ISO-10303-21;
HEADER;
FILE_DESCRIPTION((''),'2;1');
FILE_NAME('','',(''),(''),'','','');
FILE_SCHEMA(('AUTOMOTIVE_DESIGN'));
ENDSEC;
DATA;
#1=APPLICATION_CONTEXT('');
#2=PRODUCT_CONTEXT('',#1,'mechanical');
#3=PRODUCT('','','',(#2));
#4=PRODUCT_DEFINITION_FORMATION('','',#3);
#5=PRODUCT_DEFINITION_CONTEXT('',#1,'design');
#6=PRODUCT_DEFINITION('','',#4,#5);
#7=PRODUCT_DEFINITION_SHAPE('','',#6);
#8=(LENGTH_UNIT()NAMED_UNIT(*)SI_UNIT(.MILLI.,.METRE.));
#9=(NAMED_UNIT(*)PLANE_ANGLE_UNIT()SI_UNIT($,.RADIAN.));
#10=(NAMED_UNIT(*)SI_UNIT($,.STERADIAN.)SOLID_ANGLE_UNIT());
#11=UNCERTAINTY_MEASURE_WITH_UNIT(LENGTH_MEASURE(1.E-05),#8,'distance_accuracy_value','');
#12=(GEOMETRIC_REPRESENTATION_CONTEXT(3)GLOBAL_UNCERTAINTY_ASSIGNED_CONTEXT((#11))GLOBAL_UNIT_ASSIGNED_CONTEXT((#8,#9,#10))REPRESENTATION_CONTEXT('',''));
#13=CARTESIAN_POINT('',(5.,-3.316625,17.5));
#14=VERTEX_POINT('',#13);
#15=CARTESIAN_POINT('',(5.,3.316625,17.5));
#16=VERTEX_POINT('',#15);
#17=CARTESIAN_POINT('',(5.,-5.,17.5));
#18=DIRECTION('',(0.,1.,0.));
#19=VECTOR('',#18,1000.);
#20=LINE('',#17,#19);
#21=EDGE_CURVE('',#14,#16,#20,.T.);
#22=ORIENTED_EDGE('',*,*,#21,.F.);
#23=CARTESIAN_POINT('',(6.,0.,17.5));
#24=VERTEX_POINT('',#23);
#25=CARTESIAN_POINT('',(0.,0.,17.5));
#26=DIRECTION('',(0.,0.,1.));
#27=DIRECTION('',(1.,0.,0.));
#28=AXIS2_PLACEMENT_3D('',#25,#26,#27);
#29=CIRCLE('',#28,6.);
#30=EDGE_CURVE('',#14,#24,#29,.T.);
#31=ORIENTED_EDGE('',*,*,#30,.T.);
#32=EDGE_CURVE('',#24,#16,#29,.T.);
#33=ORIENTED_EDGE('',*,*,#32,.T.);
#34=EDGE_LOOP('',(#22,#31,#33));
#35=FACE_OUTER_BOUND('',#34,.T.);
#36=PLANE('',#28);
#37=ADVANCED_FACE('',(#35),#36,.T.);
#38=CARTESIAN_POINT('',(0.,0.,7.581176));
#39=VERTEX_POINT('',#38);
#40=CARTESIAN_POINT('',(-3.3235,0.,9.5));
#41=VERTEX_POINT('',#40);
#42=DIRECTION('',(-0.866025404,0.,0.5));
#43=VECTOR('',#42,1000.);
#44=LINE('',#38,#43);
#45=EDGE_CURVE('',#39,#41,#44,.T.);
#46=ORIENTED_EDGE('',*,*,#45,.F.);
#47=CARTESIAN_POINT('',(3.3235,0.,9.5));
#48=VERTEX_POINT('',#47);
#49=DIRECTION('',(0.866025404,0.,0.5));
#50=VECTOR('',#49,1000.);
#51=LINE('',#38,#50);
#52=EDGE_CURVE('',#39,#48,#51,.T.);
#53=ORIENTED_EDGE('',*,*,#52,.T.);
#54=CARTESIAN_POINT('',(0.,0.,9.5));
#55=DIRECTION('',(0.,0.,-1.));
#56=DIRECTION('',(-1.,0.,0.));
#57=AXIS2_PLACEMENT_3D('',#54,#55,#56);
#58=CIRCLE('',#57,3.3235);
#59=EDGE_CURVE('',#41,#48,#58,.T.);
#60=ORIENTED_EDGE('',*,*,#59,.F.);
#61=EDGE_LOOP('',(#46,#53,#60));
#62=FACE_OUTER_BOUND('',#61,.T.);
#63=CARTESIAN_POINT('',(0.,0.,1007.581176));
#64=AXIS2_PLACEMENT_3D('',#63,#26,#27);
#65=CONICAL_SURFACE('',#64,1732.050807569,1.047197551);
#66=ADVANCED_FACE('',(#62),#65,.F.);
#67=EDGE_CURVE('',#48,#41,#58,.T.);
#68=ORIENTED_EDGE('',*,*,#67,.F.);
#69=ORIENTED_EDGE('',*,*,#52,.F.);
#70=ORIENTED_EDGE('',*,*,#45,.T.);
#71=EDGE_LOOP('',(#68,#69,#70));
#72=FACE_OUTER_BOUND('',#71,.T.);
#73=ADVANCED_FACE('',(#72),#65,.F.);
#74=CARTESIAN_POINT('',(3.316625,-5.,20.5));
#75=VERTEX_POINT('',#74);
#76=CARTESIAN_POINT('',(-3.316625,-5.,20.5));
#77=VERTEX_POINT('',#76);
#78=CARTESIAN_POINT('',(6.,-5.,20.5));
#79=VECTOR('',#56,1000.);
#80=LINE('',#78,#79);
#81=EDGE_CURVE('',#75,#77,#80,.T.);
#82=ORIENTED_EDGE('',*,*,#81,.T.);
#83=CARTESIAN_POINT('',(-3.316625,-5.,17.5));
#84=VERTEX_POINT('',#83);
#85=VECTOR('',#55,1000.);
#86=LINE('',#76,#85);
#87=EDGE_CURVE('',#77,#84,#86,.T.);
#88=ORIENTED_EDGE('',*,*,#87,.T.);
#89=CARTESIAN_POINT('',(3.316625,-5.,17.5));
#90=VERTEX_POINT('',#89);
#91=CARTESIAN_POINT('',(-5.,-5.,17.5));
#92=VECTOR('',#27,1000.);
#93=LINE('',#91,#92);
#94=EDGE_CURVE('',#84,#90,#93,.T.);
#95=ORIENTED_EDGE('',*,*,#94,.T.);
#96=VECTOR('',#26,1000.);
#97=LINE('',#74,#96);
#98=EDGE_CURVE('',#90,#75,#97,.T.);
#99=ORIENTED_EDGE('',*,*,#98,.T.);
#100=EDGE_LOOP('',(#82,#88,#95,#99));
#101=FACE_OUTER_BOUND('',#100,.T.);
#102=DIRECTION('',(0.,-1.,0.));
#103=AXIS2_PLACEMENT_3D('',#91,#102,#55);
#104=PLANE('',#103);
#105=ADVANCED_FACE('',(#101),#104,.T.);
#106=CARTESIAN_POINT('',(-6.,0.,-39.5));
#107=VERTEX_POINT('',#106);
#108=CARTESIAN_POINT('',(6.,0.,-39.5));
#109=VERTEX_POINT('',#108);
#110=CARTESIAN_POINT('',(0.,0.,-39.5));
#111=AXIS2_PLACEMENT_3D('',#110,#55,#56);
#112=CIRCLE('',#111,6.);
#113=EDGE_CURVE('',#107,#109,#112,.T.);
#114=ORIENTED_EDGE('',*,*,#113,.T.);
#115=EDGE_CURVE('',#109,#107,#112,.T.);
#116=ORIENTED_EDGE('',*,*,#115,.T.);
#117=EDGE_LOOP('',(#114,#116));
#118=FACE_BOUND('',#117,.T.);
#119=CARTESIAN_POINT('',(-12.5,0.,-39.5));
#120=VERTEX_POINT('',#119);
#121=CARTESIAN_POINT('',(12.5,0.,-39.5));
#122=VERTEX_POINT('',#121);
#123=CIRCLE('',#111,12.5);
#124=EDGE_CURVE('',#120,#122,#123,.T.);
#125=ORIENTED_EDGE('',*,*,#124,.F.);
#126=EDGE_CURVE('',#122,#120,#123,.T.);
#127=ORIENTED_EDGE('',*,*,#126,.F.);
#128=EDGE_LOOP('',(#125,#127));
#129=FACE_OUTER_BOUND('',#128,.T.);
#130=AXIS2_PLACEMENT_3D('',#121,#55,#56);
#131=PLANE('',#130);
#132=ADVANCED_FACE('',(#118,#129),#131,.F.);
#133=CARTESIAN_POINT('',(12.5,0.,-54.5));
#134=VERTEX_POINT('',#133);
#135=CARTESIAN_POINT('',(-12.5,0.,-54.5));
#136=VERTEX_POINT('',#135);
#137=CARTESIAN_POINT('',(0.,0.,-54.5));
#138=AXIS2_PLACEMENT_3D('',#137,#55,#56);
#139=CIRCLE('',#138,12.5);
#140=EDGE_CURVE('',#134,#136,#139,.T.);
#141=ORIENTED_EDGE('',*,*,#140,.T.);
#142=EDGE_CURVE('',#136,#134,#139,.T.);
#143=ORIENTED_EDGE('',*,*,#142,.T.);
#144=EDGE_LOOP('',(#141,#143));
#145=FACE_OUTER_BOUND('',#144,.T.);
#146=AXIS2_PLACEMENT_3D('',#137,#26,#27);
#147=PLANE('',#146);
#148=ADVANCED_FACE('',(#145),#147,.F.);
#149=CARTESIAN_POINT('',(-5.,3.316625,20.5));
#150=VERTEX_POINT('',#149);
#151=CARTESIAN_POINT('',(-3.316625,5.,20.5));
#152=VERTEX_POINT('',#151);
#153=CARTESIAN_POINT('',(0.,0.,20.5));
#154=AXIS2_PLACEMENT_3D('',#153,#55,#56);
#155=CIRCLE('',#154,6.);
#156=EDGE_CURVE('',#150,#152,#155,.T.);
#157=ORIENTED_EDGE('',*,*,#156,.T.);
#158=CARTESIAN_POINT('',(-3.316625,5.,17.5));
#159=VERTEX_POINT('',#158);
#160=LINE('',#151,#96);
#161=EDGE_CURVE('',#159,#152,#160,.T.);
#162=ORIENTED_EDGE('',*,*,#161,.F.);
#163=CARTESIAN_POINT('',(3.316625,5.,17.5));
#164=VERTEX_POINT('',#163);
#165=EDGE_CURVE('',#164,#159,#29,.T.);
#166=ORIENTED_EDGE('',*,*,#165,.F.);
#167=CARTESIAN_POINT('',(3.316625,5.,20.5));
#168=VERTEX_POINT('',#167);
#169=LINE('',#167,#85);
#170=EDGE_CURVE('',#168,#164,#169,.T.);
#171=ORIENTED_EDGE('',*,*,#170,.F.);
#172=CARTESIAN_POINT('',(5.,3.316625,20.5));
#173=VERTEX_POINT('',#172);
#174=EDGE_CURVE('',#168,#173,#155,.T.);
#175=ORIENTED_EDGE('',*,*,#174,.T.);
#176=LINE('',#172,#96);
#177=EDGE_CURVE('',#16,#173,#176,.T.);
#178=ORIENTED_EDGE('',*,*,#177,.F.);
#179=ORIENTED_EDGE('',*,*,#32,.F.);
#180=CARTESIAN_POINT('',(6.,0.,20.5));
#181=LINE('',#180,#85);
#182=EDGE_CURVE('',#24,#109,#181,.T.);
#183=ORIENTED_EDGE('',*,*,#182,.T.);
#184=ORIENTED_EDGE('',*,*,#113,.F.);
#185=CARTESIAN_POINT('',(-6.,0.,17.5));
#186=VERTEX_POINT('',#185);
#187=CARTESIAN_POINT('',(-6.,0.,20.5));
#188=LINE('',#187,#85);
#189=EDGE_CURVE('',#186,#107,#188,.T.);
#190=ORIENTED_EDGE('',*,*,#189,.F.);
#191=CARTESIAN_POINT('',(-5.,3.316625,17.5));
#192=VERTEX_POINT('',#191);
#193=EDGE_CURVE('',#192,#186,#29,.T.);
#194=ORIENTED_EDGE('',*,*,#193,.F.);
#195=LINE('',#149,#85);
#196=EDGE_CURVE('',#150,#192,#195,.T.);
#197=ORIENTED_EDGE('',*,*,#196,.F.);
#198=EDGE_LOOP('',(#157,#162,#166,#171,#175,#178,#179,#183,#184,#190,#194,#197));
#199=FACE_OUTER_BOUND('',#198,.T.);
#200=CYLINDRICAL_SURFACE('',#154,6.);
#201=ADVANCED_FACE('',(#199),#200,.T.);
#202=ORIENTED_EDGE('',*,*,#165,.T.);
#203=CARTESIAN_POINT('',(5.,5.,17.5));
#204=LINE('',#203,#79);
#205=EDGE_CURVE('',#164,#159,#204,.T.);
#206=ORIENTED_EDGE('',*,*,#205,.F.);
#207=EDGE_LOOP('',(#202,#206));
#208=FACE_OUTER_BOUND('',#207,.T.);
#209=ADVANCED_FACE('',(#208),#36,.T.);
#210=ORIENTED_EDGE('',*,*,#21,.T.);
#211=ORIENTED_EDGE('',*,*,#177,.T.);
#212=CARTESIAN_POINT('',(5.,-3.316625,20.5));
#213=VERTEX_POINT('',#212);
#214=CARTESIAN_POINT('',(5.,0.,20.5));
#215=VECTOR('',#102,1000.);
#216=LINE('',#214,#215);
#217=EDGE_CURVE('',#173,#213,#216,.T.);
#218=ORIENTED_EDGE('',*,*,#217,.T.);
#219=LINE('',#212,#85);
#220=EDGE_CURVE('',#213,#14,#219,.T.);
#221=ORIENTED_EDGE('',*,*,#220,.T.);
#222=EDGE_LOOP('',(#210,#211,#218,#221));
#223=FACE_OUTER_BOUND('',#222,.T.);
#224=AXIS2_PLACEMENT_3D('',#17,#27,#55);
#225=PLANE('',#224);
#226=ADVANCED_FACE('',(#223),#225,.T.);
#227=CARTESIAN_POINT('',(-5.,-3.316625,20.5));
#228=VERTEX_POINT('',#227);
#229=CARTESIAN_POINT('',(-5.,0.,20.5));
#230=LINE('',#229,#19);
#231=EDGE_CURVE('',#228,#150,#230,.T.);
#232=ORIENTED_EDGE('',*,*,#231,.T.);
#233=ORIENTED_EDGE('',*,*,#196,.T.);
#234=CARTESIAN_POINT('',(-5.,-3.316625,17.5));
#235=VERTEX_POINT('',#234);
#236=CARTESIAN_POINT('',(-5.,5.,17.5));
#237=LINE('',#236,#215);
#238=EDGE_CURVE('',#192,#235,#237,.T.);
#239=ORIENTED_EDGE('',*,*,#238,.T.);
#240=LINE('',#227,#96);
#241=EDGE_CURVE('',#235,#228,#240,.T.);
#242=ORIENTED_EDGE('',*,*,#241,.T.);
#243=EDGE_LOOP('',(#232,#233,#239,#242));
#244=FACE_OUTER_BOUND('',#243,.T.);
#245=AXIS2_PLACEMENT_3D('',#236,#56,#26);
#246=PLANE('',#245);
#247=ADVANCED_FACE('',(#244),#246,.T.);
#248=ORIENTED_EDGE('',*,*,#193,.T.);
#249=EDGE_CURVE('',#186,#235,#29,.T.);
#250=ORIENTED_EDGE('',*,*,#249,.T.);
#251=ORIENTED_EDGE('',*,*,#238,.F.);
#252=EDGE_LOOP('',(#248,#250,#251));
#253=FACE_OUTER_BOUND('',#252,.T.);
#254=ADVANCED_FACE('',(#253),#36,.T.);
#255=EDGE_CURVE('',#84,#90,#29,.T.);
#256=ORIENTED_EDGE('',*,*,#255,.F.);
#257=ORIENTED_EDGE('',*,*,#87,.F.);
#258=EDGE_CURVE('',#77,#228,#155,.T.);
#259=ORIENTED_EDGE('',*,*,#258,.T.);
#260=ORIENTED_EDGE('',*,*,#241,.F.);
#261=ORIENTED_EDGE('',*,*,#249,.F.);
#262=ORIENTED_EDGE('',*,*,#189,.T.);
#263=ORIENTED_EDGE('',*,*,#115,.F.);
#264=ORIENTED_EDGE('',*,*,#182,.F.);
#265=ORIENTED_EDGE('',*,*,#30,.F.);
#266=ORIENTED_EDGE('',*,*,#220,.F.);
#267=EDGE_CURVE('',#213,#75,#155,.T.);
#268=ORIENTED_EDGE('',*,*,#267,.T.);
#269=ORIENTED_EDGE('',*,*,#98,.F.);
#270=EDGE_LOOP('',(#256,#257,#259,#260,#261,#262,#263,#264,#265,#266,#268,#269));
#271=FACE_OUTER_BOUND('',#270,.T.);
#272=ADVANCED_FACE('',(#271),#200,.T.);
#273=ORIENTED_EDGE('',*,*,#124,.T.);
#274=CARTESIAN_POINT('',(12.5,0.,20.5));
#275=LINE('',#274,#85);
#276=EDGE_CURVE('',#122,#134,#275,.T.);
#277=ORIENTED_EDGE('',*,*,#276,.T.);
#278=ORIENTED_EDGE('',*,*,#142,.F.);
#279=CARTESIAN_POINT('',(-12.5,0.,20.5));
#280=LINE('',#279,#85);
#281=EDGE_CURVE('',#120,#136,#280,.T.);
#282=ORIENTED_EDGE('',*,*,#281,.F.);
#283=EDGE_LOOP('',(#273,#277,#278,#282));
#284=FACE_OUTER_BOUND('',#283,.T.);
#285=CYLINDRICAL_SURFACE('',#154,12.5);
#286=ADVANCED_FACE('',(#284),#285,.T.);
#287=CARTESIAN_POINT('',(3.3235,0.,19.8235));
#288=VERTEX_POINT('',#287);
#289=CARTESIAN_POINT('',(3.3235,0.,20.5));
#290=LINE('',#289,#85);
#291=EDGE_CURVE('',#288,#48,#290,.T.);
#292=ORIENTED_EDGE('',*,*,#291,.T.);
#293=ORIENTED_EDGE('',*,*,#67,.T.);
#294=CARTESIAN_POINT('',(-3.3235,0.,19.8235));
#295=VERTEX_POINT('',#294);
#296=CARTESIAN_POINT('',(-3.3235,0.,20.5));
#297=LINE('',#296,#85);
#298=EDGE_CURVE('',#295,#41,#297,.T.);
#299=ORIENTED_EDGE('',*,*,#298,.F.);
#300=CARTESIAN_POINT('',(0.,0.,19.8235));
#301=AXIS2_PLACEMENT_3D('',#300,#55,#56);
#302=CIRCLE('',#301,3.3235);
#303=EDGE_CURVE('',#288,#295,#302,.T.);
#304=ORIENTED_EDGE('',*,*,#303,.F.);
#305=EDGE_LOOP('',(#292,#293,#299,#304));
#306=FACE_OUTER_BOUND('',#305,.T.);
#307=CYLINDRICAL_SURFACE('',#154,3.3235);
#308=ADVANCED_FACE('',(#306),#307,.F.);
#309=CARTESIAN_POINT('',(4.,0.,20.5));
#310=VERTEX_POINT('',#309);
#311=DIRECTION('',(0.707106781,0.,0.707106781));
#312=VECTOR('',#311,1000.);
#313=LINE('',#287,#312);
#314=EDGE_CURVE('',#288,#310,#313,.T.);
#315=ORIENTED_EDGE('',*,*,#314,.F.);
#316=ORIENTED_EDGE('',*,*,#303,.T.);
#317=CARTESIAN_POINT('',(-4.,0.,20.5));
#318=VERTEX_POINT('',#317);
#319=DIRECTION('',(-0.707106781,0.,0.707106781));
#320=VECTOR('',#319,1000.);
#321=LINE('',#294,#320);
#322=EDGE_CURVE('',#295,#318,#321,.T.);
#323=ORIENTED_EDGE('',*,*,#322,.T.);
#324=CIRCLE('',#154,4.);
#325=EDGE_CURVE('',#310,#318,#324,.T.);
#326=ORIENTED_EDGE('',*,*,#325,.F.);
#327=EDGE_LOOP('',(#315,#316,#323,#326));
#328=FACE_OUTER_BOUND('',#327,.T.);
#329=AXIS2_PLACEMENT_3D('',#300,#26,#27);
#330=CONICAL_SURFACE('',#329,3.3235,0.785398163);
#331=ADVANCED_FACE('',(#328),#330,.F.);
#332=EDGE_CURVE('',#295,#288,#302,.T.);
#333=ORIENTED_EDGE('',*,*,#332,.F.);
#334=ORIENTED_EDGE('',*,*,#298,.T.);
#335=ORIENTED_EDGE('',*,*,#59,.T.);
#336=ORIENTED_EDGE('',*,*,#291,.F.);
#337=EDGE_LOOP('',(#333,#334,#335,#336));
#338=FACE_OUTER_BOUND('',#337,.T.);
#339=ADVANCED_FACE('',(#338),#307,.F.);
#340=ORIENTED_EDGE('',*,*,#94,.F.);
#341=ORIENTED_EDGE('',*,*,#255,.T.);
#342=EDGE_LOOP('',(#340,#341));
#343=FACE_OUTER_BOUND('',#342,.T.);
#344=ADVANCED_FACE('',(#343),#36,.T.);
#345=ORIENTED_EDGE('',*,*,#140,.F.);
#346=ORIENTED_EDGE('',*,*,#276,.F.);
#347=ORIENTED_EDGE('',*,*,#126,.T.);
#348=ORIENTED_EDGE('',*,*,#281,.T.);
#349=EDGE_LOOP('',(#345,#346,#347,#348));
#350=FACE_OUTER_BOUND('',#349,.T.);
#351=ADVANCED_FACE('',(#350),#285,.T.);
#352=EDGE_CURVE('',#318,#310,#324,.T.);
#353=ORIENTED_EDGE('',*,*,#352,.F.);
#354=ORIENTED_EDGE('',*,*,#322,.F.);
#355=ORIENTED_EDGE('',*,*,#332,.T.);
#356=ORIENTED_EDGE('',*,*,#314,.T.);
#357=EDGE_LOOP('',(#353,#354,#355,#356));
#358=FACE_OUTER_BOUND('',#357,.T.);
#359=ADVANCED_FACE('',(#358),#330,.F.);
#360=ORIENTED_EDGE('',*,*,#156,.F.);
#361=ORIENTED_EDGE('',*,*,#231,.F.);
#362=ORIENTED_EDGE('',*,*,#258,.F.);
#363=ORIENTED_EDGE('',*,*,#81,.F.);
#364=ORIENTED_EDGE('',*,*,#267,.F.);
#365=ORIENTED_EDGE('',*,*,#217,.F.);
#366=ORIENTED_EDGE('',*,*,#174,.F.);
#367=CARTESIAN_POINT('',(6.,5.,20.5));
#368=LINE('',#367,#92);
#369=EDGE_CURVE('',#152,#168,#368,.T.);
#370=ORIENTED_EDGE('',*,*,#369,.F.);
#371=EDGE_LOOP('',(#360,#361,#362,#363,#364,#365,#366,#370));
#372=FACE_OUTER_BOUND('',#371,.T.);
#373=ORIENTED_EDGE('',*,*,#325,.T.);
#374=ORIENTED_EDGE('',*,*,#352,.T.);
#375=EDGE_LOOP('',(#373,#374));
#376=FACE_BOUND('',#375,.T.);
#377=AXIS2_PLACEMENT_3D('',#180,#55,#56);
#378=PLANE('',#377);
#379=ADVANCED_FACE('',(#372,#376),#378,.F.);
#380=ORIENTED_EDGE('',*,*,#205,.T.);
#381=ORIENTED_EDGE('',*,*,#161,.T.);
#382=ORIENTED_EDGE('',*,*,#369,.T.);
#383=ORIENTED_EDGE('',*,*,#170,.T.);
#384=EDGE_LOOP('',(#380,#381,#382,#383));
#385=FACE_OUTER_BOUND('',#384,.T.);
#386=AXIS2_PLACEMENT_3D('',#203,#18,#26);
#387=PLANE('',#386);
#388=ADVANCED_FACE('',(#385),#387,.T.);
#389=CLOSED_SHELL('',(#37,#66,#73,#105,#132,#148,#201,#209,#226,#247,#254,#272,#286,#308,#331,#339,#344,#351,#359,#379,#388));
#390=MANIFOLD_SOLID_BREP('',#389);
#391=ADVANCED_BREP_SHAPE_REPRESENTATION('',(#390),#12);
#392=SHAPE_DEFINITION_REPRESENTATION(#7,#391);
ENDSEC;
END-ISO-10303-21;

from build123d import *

# Parameters (mm, degrees)
SKETCH_2_R          = 10
SKETCH_2_W          = 10
SKETCH_2_H          = 10
CUT_EXTRUDE_1_DEPTH = 3


with BuildPart() as part:
    # 草图1 → 旋转1 (revolve)
    with BuildSketch(Plane(origin=(0, 0, 0), x_dir=(1, 0, 0), z_dir=(0, 1, 0)), mode=Mode.PRIVATE) as revolve_1_sk:
        Polygon((0, 54.5), (12.5, 54.5), (12.5, 39.5), (6, 39.5), (6, -20.5), (4, -20.5), (3.3235, -19.8235), (3.3235, -9.5), (0, -7.58117638), align=None)
    revolve(revolve_1_sk.sketch.rotate(Axis((0, 0, 20.5), (0, 0, -1)), 180), axis=Axis((0, 0, 20.5), (0, 0, -1)))

    # 草图2 → 切除-拉伸1 (cut)
    with BuildSketch(Plane.XY.offset(20.5)):
        Circle(SKETCH_2_R)
        Rectangle(SKETCH_2_W, SKETCH_2_H, mode=Mode.SUBTRACT)
    extrude(amount=-CUT_EXTRUDE_1_DEPTH, mode=Mode.SUBTRACT)


solid = part.part
